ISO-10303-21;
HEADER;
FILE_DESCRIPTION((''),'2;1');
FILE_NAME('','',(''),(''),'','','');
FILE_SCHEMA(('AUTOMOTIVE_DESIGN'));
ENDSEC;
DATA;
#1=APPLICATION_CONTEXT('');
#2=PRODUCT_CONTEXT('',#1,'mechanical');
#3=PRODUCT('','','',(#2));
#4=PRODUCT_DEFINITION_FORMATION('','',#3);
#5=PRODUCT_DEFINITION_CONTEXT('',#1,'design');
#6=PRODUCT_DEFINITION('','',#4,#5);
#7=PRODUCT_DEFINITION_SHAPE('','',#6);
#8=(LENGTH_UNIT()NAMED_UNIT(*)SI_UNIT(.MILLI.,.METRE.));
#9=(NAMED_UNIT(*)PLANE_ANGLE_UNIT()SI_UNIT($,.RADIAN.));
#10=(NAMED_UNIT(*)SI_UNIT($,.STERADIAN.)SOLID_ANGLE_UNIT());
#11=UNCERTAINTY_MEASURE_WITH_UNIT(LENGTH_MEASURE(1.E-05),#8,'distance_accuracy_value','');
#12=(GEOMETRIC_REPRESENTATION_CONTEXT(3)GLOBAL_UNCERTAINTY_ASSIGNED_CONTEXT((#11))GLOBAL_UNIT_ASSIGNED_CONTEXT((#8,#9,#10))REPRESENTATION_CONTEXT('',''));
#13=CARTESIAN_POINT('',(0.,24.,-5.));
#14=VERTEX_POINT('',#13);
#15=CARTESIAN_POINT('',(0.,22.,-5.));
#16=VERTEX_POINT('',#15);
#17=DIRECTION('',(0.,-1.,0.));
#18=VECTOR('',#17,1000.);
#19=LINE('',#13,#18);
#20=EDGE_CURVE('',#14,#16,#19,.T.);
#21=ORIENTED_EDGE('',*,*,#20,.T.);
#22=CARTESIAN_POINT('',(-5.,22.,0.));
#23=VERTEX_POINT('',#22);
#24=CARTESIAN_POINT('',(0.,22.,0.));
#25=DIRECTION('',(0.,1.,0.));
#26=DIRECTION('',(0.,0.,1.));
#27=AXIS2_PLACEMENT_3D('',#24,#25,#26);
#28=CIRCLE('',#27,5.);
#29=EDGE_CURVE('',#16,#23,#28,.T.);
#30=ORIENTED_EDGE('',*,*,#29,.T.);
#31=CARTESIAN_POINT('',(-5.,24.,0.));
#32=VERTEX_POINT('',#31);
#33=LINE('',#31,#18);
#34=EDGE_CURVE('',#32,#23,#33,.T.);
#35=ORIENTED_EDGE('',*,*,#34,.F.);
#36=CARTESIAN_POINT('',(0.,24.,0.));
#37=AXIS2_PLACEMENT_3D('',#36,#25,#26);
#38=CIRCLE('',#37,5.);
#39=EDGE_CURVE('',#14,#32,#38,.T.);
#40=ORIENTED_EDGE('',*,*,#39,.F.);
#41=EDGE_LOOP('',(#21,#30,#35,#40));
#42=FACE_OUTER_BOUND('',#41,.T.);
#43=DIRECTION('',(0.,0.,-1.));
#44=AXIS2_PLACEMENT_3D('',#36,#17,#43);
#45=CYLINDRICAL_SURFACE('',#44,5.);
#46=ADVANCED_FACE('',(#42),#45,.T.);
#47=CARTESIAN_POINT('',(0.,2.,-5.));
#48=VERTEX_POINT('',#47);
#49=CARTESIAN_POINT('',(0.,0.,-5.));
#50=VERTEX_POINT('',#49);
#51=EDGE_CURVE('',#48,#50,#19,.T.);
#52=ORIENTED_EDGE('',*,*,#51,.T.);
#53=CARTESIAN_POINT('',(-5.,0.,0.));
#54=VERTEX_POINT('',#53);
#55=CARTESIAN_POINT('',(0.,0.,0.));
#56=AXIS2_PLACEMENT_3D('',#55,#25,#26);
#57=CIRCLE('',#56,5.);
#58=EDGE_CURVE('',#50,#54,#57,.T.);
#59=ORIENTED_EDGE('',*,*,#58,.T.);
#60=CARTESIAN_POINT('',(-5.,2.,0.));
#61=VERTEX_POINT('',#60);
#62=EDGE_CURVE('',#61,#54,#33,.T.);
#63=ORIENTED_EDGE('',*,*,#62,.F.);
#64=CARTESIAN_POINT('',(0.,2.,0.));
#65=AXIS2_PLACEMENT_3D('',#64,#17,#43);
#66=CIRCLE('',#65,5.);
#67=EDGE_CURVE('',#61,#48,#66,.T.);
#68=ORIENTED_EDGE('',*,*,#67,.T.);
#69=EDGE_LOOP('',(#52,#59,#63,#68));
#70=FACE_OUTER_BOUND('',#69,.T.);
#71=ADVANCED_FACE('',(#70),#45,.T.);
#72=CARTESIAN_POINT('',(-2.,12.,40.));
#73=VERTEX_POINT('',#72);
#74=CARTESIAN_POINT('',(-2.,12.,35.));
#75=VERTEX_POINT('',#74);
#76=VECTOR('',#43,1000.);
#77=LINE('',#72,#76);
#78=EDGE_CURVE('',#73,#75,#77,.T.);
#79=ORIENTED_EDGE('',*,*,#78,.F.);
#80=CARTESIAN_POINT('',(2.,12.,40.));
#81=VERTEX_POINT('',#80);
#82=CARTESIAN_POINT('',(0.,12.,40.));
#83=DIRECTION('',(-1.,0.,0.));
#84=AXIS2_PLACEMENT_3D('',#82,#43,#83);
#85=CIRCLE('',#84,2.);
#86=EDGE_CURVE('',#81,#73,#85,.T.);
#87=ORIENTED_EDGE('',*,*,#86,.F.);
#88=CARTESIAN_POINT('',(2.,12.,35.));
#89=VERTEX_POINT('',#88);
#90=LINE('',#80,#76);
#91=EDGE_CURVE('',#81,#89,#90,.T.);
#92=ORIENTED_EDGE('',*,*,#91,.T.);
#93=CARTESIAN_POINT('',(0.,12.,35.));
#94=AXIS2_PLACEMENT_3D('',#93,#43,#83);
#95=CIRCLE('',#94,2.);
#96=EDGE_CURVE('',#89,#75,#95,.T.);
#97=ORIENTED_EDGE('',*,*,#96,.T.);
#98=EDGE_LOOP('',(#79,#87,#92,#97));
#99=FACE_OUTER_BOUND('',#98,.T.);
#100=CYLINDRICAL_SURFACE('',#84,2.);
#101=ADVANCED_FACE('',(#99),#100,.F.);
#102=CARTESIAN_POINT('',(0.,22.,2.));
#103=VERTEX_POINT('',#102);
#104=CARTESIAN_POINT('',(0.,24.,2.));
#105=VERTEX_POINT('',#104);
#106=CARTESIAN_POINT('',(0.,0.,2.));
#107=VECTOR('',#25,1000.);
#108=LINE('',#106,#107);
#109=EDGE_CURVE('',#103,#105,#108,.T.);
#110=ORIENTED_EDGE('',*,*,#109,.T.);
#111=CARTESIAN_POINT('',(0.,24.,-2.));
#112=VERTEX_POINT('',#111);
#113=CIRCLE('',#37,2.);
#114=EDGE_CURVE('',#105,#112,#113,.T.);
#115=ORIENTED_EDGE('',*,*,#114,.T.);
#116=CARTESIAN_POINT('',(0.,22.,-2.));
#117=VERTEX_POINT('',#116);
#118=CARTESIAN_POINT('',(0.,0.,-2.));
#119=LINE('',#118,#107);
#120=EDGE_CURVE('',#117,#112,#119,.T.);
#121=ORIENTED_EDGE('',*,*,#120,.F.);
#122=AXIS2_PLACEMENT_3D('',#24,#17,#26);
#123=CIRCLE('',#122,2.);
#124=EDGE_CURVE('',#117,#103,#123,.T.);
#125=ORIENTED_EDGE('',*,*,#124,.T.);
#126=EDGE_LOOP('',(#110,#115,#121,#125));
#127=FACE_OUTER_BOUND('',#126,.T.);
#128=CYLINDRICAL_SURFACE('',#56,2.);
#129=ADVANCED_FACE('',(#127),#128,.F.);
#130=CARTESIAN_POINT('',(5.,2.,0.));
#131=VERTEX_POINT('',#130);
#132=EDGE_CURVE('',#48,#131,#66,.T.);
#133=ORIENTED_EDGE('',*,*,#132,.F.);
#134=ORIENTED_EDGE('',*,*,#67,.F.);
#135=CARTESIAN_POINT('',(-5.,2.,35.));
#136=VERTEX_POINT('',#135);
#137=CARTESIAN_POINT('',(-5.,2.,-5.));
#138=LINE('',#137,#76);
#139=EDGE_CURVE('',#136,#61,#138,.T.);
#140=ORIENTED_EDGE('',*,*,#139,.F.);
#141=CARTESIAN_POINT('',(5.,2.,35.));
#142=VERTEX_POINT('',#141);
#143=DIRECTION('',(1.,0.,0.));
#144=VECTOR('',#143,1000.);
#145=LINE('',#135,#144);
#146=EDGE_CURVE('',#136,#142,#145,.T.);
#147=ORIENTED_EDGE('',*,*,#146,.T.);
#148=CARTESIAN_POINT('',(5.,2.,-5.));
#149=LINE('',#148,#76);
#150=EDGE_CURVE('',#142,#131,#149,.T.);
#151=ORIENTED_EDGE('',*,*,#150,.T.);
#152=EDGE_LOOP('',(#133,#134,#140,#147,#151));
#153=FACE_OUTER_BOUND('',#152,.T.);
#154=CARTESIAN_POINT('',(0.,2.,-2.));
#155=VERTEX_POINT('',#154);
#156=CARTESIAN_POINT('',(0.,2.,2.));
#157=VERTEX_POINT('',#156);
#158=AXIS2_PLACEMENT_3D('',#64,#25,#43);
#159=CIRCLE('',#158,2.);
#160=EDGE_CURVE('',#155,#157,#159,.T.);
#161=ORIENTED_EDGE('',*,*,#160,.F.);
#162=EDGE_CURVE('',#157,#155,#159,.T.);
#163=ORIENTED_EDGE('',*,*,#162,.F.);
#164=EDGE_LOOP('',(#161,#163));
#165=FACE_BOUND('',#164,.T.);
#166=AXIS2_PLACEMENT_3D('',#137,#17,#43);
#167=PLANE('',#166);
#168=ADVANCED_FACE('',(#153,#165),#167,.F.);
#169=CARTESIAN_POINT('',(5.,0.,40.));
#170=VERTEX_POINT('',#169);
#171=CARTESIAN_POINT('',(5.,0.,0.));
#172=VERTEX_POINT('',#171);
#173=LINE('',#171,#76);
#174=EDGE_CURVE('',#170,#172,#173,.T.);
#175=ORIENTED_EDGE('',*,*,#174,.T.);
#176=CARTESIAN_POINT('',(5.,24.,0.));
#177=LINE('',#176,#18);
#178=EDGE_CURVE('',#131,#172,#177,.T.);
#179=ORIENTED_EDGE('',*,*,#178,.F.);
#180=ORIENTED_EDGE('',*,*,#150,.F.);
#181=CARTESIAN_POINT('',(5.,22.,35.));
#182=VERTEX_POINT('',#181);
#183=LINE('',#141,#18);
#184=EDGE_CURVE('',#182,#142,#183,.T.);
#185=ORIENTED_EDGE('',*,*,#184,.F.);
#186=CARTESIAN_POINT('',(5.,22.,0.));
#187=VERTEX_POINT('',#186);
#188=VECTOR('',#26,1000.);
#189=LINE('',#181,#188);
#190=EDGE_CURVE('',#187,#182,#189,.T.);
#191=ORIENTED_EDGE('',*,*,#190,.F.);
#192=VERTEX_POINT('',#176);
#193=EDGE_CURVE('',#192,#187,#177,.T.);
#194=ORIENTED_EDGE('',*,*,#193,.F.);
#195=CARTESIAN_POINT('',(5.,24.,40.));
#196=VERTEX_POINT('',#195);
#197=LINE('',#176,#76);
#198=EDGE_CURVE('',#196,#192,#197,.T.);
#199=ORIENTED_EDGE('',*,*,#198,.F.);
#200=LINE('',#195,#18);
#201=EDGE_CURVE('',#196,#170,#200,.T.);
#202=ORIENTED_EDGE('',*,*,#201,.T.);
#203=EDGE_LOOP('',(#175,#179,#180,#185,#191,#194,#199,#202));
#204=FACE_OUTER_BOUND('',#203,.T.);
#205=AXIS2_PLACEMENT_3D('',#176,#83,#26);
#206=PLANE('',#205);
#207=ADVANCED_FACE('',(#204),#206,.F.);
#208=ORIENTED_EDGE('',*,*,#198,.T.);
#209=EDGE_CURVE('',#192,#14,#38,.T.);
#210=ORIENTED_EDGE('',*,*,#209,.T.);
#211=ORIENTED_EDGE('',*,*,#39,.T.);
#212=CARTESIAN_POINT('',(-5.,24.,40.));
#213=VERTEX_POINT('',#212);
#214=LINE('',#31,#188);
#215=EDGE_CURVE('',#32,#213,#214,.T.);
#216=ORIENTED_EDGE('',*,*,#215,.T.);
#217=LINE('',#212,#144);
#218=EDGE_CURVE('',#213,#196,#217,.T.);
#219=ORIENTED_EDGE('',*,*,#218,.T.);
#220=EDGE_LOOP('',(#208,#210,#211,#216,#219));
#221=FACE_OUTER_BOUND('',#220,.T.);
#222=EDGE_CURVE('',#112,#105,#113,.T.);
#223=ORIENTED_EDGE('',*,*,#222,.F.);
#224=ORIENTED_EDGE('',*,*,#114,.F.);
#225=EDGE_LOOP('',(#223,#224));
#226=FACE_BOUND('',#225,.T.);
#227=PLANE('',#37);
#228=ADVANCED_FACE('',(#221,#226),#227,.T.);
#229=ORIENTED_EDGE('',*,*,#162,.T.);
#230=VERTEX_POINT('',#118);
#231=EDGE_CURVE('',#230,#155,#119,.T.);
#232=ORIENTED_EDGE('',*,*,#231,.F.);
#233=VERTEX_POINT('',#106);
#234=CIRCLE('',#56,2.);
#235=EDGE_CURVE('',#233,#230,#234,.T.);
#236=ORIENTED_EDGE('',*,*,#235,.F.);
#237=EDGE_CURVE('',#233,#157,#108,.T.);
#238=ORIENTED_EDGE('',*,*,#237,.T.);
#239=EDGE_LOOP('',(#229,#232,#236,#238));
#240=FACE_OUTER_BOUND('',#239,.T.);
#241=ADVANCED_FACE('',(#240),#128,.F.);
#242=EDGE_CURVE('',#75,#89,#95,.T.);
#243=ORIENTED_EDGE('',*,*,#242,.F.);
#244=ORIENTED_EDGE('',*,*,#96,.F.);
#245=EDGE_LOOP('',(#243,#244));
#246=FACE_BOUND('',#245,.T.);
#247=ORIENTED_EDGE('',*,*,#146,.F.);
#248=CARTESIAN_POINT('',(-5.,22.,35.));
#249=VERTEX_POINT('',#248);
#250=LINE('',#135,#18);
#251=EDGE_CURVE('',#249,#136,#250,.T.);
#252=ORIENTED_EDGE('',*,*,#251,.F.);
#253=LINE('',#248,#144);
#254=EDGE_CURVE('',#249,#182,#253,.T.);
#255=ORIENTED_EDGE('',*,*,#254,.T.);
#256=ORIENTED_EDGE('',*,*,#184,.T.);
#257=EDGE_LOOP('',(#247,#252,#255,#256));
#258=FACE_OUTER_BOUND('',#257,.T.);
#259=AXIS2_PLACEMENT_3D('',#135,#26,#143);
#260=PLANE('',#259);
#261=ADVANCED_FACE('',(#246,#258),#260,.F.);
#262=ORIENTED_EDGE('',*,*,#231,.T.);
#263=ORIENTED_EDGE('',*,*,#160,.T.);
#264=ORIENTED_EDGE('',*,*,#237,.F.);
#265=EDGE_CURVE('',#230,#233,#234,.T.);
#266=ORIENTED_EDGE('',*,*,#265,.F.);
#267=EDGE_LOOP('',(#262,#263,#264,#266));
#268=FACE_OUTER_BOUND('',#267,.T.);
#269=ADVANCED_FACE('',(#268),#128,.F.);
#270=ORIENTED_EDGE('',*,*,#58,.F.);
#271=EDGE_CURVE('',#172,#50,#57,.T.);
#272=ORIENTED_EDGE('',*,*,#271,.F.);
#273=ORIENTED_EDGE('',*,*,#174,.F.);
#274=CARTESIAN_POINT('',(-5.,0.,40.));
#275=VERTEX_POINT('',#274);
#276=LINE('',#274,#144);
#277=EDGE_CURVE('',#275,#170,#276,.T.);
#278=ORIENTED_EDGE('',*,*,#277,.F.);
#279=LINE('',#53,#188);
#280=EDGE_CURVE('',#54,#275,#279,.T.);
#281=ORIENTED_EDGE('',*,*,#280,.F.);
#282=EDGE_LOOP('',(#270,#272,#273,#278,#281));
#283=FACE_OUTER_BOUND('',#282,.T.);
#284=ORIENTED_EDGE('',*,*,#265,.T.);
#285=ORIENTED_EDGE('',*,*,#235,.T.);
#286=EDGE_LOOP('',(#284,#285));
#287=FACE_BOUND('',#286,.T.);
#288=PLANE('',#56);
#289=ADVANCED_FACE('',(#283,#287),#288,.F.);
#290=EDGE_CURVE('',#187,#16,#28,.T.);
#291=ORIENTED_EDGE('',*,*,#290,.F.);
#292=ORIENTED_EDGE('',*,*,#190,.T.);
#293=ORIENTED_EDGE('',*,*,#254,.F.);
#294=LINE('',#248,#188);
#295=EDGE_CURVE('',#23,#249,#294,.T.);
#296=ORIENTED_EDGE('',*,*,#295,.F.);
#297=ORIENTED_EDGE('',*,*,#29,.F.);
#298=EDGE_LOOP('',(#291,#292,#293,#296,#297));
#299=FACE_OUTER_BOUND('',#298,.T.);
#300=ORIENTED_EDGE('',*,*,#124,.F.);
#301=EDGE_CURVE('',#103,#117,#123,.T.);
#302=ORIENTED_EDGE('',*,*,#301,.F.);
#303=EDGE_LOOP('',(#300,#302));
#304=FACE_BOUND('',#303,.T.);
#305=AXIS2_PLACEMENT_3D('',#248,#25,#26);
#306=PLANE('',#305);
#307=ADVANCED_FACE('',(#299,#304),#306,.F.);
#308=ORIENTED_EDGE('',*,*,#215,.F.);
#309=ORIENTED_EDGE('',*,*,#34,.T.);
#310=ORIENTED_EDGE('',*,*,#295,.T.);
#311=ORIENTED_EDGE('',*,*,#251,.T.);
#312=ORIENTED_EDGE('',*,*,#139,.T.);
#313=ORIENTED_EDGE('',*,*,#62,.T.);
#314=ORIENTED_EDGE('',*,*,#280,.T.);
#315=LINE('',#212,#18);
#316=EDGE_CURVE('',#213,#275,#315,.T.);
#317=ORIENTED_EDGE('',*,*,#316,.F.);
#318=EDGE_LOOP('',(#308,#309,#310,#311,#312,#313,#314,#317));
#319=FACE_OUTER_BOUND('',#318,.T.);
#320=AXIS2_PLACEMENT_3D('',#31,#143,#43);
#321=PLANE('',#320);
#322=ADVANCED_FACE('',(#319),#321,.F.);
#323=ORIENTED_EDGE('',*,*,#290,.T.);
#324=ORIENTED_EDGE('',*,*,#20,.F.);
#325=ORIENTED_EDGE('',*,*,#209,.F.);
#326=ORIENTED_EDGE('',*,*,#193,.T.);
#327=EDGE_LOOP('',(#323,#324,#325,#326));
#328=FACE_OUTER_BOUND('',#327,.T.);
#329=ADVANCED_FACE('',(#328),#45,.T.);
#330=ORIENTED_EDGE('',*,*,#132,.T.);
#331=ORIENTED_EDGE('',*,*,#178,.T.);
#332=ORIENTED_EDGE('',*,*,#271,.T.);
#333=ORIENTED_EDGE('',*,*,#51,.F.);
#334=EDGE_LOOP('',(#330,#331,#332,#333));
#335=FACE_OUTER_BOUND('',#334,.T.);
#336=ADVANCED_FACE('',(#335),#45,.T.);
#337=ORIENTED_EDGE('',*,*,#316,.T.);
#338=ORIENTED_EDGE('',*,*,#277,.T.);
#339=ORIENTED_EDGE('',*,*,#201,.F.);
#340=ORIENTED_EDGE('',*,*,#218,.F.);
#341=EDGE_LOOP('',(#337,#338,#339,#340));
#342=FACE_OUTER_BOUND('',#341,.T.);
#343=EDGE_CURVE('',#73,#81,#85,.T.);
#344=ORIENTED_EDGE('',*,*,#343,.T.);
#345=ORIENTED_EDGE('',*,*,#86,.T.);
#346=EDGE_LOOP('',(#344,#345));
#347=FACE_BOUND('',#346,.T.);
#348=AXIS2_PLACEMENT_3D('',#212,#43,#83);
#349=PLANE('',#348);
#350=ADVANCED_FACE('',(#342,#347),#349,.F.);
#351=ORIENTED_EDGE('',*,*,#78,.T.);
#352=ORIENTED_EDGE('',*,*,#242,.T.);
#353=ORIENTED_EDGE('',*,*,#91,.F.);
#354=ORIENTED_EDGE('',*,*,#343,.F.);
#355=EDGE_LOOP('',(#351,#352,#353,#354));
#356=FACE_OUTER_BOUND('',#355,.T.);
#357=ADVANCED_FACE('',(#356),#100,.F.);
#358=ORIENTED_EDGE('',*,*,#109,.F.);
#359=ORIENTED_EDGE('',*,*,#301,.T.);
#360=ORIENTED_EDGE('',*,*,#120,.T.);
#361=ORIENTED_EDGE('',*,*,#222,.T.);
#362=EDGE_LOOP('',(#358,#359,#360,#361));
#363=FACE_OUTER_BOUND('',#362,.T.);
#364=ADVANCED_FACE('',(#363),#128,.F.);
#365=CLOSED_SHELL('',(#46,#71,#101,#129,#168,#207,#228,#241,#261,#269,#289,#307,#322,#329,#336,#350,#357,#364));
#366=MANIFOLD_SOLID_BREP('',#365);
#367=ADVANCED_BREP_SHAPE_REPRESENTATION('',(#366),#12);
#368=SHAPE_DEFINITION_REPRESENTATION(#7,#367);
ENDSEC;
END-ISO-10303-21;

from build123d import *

# Parameters (mm, degrees)
BOSS_EXTRUDE1_DEPTH     = 24
CUT_EXTRUDE1_DEPTH      = 47.914816423
CUT_EXTRUDE1_DEPTH_BACK = 47.914816423
SKETCH2_R               = 2
SKETCH3_W               = 40
SKETCH3_H               = 20
CUT_EXTRUDE2_DEPTH      = 48.707441768
SKETCH4_R               = 2
CUT_EXTRUDE3_DEPTH      = 47.914816423


with BuildPart() as part:
    # Sketch1 → Boss-Extrude1 (new body)
    with BuildSketch(Plane(origin=(0, 0, 0), x_dir=(1, 0, 0), z_dir=(0, 1, 0))):
        with BuildLine():
            Line((-5, 0), (-5, -40))
            Line((-5, -40), (5, -40))
            Line((5, -40), (5, 0))
            ThreePointArc((5, 0), (0, 5), (-5, 0))
        make_face()
    extrude(amount=BOSS_EXTRUDE1_DEPTH)

    # Sketch2 → Cut-Extrude1 (cut, two sides: drawn at the far end of the back side and taken through both)
    with BuildSketch(Plane(origin=(0, 24, 0), x_dir=(1, 0, 0), z_dir=(0, 1, 0)).offset(-CUT_EXTRUDE1_DEPTH_BACK)):
        with Locations(Location((0, 0, 0), (0, 0, 270))):
            Circle(SKETCH2_R)
    extrude(amount=CUT_EXTRUDE1_DEPTH + CUT_EXTRUDE1_DEPTH_BACK, mode=Mode.SUBTRACT)

    # Sketch3 → Cut-Extrude2 (cut, through all)
    with BuildSketch(Plane(origin=(5, 0, 0), x_dir=(0, 0, -1), z_dir=(1, 0, 0))):
        with Locations((-15, 12)):
            Rectangle(SKETCH3_W, SKETCH3_H)
    extrude(amount=-CUT_EXTRUDE2_DEPTH, mode=Mode.SUBTRACT)

    # Sketch4 → Cut-Extrude3 (cut, through all)
    with BuildSketch(Plane(origin=(0, 0, 35), x_dir=(-1, 0, 0), z_dir=(0, 0, -1))):
        with Locations((0, 12)):
            Circle(SKETCH4_R)
    extrude(amount=-CUT_EXTRUDE3_DEPTH, mode=Mode.SUBTRACT)


solid = part.part
